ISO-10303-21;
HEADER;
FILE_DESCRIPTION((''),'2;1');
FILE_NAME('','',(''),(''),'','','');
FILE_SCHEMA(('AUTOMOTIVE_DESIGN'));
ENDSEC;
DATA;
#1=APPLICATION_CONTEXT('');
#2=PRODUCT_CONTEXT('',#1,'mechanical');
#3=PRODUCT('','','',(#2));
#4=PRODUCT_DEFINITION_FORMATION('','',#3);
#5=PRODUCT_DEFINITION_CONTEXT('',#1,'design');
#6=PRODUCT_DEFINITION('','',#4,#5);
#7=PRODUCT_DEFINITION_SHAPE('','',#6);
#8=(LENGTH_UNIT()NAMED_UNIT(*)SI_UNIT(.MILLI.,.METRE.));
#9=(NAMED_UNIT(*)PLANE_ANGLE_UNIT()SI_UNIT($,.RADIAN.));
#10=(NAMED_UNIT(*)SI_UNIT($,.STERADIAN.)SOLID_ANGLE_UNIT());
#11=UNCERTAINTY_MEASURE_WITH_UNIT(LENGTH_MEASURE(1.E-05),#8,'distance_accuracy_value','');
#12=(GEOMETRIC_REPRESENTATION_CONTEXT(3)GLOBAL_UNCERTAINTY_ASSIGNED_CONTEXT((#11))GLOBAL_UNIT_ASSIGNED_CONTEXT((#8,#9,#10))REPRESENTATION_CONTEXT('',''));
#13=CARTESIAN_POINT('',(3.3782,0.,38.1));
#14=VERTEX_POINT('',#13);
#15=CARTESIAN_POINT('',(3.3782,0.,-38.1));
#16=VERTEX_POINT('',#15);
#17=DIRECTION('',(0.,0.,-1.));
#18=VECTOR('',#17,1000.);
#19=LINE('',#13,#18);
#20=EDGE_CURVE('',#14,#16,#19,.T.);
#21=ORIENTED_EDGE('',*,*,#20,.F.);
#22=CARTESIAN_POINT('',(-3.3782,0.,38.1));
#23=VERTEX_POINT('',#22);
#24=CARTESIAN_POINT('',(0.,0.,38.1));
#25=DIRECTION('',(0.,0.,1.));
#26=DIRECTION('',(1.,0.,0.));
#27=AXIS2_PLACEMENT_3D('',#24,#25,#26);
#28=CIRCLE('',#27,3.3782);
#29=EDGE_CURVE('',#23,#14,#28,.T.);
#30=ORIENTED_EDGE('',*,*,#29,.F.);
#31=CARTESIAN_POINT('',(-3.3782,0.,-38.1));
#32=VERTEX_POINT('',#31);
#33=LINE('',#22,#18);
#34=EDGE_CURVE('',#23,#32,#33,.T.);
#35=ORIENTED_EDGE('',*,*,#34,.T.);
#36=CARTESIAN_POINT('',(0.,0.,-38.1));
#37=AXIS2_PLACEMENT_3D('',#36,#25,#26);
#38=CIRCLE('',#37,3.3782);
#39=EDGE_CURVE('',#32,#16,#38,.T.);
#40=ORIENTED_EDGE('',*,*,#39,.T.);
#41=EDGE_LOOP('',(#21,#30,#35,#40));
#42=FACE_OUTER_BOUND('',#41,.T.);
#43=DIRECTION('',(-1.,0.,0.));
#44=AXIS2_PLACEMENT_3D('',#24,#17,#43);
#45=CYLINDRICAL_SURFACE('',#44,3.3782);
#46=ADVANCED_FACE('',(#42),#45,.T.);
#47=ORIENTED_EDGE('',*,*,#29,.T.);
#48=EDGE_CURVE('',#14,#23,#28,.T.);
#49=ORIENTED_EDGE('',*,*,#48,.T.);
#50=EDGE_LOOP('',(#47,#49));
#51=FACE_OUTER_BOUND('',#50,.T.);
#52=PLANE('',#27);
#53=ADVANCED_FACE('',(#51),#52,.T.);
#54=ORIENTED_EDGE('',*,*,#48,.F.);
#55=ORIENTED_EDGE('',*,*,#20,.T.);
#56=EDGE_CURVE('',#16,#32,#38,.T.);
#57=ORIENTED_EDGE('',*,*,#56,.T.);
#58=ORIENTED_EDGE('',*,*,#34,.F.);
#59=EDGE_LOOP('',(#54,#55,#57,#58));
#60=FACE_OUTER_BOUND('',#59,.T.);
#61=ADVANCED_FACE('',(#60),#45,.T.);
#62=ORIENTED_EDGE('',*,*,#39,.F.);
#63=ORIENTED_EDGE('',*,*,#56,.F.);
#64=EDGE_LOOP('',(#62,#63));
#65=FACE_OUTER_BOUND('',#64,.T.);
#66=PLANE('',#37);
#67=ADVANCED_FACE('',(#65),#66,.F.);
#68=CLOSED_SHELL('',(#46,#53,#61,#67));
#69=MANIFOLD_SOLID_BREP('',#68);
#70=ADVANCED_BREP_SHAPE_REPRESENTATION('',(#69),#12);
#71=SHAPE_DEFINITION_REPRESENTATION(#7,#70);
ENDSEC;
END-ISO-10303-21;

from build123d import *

# Parameters (mm, degrees)
BOSS_EXTRUDE1_DEPTH      = 38.1
BOSS_EXTRUDE1_DEPTH_BACK = 38.1
SKETCH2_R                = 3.3782


with BuildPart() as part:
    # Sketch2 → Boss-Extrude1 (new, two sides: drawn at the far end of the back side and taken through both)
    with BuildSketch(Plane.XY.offset(-BOSS_EXTRUDE1_DEPTH_BACK)):
        with Locations(Location((0, 0, 0), (0, 0, 180))):
            Circle(SKETCH2_R)
    extrude(amount=BOSS_EXTRUDE1_DEPTH + BOSS_EXTRUDE1_DEPTH_BACK)


solid = part.part
